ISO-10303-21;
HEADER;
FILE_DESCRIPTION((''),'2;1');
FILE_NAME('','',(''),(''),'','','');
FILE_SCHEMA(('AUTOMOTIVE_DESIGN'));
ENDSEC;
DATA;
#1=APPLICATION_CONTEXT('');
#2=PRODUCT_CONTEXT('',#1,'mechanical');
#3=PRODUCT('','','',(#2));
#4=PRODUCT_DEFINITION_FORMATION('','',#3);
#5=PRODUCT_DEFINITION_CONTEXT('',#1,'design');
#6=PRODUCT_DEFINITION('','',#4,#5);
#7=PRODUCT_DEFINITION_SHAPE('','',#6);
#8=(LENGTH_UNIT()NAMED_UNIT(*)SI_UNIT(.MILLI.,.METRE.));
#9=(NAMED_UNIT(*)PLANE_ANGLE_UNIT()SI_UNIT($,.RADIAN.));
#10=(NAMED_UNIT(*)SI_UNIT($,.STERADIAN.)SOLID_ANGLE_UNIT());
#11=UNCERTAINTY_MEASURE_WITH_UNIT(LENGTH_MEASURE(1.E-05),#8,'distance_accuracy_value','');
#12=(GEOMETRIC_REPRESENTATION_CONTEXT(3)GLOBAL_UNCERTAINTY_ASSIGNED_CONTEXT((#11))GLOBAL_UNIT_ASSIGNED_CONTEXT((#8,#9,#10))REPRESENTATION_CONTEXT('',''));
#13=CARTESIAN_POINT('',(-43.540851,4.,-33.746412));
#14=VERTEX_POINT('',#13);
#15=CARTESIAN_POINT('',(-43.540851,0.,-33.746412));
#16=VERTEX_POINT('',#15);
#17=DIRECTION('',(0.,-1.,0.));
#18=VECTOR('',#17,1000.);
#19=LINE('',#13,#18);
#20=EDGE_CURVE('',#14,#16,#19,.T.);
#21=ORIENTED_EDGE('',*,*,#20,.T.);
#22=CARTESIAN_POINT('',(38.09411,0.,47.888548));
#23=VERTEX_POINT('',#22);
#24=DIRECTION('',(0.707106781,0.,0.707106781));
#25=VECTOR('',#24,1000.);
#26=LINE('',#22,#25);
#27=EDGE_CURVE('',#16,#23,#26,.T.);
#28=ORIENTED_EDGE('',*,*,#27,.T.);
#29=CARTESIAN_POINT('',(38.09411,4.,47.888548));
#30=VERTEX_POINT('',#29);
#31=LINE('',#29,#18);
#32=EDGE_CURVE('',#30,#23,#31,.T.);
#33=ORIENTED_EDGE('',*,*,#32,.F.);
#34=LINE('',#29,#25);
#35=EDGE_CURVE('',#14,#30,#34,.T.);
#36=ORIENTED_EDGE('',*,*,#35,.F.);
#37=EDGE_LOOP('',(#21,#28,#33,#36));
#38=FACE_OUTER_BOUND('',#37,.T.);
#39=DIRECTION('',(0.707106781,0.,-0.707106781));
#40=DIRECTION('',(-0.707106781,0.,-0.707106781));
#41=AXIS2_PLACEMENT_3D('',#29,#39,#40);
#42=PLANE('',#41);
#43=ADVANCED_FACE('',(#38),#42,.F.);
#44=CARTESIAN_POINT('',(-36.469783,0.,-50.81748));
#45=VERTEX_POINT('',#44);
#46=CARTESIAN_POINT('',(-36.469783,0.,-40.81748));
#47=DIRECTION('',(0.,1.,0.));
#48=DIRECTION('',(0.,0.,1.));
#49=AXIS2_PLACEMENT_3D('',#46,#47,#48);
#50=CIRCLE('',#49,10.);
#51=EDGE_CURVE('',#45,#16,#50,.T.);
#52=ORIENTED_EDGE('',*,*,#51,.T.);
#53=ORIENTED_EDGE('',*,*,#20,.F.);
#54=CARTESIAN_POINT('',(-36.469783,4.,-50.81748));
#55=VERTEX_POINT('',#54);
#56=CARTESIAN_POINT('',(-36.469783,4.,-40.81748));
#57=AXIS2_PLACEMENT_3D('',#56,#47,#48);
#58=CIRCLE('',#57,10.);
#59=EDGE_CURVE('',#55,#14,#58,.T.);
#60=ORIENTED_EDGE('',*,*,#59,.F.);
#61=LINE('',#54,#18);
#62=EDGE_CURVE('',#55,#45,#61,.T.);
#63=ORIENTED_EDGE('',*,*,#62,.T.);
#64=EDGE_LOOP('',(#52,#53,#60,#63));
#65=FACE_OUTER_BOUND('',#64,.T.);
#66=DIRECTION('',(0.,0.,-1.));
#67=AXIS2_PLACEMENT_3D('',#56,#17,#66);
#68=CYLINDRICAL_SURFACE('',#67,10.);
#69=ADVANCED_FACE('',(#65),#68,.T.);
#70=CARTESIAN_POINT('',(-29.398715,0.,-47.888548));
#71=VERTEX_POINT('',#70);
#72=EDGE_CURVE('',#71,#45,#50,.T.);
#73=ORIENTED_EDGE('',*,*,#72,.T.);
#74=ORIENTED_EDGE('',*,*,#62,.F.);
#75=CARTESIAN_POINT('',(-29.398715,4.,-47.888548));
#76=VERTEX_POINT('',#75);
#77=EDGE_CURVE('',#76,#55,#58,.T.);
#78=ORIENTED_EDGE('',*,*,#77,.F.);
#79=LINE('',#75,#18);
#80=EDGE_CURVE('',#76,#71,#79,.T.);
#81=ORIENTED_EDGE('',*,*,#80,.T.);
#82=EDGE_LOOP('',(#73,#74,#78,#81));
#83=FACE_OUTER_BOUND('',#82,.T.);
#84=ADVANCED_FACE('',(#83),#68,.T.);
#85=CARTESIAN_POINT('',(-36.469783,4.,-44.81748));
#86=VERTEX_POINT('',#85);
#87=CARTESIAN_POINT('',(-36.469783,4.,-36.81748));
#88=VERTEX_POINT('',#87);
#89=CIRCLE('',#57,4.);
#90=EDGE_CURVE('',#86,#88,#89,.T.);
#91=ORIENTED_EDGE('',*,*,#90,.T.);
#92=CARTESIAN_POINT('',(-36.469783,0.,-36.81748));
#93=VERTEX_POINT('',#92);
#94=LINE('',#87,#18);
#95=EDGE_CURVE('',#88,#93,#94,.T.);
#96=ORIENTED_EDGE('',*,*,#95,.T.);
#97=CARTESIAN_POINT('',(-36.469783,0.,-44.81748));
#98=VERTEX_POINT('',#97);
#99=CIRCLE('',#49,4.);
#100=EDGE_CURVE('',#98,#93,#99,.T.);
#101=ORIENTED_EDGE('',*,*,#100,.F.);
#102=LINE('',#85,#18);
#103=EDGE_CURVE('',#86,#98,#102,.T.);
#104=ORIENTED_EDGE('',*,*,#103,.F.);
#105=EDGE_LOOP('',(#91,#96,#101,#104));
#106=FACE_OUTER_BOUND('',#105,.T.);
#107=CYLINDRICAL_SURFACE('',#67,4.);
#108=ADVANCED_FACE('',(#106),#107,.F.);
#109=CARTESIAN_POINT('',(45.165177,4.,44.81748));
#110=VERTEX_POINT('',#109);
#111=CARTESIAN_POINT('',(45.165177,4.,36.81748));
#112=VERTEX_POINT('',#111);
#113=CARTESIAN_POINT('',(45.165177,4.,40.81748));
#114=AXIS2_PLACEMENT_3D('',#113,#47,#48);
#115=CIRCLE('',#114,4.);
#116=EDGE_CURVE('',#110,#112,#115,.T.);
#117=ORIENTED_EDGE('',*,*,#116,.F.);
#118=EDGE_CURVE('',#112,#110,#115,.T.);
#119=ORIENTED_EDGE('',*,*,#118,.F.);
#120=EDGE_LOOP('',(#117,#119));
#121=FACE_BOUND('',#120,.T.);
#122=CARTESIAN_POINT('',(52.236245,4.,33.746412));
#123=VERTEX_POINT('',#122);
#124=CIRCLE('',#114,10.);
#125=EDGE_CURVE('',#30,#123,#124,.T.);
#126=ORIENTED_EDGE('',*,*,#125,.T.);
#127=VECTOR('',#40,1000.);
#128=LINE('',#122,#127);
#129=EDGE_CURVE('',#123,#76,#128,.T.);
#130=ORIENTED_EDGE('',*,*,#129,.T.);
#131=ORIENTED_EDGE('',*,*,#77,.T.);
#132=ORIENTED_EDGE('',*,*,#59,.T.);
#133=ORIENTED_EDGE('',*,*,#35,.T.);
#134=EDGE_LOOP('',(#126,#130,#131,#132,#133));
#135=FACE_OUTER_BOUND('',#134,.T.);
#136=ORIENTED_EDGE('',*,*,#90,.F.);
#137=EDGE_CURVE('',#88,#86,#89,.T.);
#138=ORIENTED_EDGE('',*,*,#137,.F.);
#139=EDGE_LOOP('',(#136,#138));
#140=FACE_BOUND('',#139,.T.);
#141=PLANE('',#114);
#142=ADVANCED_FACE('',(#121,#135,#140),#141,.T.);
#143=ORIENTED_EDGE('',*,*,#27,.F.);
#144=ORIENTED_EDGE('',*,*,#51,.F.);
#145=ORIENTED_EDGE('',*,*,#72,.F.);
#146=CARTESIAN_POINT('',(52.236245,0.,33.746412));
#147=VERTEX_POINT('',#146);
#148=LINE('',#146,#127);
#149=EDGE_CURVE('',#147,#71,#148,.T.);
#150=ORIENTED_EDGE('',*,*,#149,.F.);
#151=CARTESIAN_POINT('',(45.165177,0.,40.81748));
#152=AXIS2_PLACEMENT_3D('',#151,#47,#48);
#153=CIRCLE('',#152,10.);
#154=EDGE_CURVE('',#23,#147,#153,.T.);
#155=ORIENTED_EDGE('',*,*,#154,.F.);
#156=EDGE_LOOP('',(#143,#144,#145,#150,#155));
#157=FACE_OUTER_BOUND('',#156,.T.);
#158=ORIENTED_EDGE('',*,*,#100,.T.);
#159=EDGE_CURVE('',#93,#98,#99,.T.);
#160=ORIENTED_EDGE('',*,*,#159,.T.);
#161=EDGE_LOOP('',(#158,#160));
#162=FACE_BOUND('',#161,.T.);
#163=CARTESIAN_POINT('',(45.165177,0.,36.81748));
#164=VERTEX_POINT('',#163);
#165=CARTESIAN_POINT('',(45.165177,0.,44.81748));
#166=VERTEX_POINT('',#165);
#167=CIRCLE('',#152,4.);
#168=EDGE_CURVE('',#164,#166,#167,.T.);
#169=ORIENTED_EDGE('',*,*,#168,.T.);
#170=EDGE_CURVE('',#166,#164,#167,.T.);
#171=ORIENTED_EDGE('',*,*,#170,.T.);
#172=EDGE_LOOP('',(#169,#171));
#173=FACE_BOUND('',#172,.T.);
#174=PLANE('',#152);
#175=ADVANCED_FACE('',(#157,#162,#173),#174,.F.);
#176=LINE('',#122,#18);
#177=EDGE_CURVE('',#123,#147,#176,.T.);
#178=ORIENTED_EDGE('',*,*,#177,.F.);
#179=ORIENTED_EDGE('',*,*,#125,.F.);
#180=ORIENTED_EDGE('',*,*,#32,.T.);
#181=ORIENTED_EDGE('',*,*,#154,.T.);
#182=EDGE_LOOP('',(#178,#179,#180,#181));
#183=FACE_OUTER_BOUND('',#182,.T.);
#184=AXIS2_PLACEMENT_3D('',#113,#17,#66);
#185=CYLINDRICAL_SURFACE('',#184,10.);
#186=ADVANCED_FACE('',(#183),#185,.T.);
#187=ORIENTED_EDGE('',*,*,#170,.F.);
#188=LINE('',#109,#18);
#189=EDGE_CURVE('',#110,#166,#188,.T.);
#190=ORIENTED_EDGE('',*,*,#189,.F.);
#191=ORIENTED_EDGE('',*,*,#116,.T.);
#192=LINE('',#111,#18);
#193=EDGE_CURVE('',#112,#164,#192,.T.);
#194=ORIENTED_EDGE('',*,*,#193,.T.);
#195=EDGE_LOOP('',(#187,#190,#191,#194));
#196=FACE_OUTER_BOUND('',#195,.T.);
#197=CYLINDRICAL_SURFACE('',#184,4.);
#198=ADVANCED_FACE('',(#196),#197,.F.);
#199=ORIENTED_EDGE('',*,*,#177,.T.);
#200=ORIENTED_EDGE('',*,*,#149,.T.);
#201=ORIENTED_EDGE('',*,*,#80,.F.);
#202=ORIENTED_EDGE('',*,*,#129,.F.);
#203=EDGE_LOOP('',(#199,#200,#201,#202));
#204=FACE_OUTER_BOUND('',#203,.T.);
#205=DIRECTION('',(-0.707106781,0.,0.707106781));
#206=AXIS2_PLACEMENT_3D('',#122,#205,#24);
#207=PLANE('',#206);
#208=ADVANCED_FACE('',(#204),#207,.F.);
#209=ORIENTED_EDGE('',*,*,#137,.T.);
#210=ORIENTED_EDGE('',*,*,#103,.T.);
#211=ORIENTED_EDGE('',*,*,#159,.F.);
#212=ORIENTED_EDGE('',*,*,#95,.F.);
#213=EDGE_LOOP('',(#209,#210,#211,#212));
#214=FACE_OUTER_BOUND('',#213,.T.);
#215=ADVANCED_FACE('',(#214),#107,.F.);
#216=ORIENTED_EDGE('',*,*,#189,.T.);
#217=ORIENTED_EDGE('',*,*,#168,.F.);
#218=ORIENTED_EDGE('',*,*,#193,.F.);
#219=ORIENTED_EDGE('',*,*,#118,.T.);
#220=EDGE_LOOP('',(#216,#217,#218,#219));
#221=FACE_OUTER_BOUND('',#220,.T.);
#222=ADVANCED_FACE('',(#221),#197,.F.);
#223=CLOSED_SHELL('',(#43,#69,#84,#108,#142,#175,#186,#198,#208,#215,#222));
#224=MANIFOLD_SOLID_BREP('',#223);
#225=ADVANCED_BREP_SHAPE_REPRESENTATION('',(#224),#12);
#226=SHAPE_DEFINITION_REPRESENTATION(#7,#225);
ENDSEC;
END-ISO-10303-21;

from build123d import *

# Parameters (mm, degrees)
SKETCH1_R          = 4
BOSS_EXTRU_1_DEPTH = 4


with BuildPart() as part:
    # Sketch1 → Boss.-Extru.1 (new body)
    with BuildSketch(Plane(origin=(0, 0, 0), x_dir=(1, 0, 0), z_dir=(0, 1, 0))):
        with BuildLine():
            Line((38.094109607, -47.888548123), (-43.540851016, 33.7464125))
            ThreePointArc((-43.540851016, 33.7464125), (-43.540851016, 47.888548123), (-29.398715392, 47.888548123))
            Line((-29.398715392, 47.888548123), (52.236245231, -33.7464125))
            ThreePointArc((52.236245231, -33.7464125), (52.236245231, -47.888548123), (38.094109607, -47.888548123))
        make_face()
        with Locations(Location((45.165177419, -40.817480312, 0), (0, 0, 270))):
            Circle(SKETCH1_R, mode=Mode.SUBTRACT)
        with Locations(Location((-36.469783204, 40.817480312, 0), (0, 0, 270))):
            Circle(SKETCH1_R, mode=Mode.SUBTRACT)
    extrude(amount=BOSS_EXTRU_1_DEPTH)


solid = part.part
